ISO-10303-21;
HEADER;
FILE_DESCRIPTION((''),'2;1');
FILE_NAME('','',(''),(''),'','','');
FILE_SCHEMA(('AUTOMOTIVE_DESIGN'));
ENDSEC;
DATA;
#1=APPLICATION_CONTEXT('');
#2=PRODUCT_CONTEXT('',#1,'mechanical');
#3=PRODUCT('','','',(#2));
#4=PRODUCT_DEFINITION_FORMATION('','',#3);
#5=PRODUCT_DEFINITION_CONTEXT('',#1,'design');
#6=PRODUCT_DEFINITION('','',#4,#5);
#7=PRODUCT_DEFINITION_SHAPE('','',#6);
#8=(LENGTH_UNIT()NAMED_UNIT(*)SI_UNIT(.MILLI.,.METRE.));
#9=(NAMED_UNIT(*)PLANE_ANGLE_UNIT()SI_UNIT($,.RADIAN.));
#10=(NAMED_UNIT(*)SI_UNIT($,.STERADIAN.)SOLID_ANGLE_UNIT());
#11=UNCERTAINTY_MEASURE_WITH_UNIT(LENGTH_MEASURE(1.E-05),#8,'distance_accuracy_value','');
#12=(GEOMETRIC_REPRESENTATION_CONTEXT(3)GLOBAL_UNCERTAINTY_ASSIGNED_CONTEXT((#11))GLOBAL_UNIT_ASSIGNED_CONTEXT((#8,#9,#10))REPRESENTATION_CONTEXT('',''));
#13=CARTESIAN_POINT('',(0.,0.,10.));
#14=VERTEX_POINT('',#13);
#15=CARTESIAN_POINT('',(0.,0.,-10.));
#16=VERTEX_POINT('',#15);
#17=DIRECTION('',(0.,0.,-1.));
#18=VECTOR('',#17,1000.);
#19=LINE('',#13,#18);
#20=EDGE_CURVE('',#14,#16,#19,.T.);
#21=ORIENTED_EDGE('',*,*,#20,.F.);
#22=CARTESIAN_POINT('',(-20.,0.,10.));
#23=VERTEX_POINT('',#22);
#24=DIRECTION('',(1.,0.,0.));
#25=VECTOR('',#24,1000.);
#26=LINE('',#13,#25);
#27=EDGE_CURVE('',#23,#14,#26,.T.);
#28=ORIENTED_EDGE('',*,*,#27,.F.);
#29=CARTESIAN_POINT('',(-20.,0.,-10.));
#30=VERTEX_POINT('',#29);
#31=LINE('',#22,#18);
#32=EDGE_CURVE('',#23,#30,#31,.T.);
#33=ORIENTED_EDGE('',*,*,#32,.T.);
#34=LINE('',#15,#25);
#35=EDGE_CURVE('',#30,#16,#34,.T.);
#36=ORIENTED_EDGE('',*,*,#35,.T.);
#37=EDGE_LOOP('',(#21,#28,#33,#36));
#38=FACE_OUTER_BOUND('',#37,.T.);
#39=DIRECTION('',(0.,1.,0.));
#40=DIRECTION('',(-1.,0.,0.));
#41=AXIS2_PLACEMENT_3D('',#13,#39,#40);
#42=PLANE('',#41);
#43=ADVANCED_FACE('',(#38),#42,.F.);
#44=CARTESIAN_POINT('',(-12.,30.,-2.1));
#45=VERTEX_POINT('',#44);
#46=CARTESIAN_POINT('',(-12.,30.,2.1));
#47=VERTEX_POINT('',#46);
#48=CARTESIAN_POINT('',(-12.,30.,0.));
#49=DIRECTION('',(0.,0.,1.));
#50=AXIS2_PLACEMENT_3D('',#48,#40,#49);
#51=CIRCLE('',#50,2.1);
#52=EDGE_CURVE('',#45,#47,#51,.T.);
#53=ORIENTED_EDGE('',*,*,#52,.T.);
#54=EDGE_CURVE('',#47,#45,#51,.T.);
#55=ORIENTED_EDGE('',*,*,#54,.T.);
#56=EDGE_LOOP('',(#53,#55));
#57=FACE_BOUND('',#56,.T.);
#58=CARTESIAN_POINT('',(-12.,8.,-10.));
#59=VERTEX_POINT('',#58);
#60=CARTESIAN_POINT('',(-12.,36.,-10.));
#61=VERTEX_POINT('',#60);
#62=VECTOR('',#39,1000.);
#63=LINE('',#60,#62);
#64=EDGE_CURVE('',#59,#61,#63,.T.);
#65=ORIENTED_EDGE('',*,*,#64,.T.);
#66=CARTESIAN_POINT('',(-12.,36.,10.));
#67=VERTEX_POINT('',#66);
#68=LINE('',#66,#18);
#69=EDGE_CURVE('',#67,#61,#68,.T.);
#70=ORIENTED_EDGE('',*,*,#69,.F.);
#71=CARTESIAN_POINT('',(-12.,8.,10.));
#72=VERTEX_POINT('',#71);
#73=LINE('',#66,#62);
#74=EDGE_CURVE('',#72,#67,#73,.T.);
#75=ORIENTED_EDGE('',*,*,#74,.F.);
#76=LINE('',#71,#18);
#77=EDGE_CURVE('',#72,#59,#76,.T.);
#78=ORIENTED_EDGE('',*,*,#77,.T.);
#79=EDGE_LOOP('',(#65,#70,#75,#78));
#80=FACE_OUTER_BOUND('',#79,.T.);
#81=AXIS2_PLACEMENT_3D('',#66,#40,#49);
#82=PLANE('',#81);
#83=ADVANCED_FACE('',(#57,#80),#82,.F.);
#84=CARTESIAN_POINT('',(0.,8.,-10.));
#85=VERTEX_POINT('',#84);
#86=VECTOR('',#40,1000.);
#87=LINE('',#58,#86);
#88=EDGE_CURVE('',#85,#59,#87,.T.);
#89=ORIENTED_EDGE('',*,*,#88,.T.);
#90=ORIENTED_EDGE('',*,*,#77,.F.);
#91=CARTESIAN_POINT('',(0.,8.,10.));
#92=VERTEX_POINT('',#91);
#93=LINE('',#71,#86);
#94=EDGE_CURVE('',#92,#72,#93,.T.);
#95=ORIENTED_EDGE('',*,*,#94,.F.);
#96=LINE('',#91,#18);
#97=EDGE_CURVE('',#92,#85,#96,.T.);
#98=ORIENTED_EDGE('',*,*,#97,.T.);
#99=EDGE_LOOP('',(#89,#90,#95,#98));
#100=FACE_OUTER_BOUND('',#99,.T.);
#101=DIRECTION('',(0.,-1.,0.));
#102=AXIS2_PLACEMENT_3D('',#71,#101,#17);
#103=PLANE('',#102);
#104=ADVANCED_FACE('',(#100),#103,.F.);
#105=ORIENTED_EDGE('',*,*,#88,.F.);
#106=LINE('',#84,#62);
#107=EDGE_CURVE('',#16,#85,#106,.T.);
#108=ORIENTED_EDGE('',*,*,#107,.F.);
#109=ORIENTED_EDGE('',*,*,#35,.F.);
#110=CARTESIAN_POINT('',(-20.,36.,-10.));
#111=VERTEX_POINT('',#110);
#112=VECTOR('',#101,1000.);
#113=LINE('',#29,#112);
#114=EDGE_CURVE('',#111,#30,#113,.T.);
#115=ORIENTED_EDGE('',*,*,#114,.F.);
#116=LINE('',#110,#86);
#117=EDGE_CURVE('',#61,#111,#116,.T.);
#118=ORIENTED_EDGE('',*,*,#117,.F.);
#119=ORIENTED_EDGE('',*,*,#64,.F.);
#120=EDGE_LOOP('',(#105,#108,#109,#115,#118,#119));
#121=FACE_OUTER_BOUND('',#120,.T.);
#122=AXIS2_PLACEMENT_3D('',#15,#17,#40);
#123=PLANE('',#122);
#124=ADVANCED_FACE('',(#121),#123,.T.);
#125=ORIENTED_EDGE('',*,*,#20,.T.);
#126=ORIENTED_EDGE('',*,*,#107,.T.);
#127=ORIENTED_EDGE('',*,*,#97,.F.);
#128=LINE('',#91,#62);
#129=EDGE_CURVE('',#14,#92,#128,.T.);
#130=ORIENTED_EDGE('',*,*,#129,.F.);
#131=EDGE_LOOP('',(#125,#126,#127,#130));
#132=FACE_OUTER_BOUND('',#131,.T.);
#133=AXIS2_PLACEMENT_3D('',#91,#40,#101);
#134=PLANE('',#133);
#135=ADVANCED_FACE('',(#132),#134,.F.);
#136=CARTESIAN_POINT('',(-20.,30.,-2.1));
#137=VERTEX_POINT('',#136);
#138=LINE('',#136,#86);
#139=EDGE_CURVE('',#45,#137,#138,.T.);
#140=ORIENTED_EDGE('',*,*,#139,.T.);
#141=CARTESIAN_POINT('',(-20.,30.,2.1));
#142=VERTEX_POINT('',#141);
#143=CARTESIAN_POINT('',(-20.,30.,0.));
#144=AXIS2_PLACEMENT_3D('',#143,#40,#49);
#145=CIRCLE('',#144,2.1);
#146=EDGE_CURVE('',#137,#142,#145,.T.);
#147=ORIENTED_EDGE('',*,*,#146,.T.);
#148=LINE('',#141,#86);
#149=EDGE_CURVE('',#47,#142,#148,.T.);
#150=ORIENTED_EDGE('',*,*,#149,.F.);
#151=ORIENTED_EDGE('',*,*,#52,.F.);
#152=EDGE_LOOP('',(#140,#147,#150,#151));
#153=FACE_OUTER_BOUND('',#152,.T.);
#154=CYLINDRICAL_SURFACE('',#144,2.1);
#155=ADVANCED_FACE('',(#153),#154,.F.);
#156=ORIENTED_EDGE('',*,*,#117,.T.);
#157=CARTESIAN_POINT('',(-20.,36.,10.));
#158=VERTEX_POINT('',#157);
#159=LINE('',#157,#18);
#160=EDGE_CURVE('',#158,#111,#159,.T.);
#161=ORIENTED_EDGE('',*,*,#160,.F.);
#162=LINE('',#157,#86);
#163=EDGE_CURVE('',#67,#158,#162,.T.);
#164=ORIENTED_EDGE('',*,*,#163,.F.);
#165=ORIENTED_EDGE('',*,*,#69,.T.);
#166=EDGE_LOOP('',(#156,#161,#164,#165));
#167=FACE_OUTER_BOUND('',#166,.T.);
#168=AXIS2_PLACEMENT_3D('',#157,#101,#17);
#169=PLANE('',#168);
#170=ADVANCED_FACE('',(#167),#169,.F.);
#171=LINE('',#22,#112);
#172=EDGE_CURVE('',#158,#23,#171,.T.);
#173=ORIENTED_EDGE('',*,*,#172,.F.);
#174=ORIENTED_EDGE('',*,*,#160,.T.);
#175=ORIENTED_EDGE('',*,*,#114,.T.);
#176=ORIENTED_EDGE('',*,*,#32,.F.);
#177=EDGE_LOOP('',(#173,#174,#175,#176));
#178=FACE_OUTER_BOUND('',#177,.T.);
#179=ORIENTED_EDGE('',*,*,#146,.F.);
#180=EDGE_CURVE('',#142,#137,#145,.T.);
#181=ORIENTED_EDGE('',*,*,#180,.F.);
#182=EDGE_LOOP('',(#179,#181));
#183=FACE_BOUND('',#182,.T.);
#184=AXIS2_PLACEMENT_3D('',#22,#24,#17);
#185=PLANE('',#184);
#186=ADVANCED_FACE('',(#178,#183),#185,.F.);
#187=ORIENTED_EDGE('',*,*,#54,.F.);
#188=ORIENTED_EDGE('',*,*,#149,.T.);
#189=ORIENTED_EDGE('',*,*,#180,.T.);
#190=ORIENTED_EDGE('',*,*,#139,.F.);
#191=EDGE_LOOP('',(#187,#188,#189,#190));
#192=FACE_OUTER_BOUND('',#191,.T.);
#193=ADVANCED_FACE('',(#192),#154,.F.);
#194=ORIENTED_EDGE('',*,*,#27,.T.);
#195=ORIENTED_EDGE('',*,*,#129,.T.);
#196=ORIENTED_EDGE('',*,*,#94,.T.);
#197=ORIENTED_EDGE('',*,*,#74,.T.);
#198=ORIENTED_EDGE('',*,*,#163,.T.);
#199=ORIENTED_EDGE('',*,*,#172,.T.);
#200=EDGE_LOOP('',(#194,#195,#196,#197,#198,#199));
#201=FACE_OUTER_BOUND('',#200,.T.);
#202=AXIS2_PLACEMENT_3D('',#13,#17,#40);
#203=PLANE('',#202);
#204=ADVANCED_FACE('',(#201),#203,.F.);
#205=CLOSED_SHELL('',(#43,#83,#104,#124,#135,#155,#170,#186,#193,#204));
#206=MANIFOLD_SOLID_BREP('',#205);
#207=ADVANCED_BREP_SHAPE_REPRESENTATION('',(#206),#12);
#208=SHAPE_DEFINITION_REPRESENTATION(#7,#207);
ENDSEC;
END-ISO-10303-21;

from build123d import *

# Parameters (mm, degrees)
EXTRUDE_1_DEPTH    = 10
HOLE_WIZARD_M5_1_D = 4.2


with BuildPart() as part:
    # 草图1 → 凸台-拉伸1 (new, symmetric)
    with BuildSketch(Plane.XY):
        Polygon((0, 0), (-20, 0), (-20, 36), (-12, 36), (-12, 8), (0, 8), align=None)
    extrude(amount=EXTRUDE_1_DEPTH, both=True)

    # M5 螺纹孔1 (through all)
    with Locations(Plane(origin=(-20, 30, 0), x_dir=(0, 0, -1), z_dir=(-1, 0, 0))):
        with Locations((0, 0)):
            Hole(HOLE_WIZARD_M5_1_D / 2)


solid = part.part
